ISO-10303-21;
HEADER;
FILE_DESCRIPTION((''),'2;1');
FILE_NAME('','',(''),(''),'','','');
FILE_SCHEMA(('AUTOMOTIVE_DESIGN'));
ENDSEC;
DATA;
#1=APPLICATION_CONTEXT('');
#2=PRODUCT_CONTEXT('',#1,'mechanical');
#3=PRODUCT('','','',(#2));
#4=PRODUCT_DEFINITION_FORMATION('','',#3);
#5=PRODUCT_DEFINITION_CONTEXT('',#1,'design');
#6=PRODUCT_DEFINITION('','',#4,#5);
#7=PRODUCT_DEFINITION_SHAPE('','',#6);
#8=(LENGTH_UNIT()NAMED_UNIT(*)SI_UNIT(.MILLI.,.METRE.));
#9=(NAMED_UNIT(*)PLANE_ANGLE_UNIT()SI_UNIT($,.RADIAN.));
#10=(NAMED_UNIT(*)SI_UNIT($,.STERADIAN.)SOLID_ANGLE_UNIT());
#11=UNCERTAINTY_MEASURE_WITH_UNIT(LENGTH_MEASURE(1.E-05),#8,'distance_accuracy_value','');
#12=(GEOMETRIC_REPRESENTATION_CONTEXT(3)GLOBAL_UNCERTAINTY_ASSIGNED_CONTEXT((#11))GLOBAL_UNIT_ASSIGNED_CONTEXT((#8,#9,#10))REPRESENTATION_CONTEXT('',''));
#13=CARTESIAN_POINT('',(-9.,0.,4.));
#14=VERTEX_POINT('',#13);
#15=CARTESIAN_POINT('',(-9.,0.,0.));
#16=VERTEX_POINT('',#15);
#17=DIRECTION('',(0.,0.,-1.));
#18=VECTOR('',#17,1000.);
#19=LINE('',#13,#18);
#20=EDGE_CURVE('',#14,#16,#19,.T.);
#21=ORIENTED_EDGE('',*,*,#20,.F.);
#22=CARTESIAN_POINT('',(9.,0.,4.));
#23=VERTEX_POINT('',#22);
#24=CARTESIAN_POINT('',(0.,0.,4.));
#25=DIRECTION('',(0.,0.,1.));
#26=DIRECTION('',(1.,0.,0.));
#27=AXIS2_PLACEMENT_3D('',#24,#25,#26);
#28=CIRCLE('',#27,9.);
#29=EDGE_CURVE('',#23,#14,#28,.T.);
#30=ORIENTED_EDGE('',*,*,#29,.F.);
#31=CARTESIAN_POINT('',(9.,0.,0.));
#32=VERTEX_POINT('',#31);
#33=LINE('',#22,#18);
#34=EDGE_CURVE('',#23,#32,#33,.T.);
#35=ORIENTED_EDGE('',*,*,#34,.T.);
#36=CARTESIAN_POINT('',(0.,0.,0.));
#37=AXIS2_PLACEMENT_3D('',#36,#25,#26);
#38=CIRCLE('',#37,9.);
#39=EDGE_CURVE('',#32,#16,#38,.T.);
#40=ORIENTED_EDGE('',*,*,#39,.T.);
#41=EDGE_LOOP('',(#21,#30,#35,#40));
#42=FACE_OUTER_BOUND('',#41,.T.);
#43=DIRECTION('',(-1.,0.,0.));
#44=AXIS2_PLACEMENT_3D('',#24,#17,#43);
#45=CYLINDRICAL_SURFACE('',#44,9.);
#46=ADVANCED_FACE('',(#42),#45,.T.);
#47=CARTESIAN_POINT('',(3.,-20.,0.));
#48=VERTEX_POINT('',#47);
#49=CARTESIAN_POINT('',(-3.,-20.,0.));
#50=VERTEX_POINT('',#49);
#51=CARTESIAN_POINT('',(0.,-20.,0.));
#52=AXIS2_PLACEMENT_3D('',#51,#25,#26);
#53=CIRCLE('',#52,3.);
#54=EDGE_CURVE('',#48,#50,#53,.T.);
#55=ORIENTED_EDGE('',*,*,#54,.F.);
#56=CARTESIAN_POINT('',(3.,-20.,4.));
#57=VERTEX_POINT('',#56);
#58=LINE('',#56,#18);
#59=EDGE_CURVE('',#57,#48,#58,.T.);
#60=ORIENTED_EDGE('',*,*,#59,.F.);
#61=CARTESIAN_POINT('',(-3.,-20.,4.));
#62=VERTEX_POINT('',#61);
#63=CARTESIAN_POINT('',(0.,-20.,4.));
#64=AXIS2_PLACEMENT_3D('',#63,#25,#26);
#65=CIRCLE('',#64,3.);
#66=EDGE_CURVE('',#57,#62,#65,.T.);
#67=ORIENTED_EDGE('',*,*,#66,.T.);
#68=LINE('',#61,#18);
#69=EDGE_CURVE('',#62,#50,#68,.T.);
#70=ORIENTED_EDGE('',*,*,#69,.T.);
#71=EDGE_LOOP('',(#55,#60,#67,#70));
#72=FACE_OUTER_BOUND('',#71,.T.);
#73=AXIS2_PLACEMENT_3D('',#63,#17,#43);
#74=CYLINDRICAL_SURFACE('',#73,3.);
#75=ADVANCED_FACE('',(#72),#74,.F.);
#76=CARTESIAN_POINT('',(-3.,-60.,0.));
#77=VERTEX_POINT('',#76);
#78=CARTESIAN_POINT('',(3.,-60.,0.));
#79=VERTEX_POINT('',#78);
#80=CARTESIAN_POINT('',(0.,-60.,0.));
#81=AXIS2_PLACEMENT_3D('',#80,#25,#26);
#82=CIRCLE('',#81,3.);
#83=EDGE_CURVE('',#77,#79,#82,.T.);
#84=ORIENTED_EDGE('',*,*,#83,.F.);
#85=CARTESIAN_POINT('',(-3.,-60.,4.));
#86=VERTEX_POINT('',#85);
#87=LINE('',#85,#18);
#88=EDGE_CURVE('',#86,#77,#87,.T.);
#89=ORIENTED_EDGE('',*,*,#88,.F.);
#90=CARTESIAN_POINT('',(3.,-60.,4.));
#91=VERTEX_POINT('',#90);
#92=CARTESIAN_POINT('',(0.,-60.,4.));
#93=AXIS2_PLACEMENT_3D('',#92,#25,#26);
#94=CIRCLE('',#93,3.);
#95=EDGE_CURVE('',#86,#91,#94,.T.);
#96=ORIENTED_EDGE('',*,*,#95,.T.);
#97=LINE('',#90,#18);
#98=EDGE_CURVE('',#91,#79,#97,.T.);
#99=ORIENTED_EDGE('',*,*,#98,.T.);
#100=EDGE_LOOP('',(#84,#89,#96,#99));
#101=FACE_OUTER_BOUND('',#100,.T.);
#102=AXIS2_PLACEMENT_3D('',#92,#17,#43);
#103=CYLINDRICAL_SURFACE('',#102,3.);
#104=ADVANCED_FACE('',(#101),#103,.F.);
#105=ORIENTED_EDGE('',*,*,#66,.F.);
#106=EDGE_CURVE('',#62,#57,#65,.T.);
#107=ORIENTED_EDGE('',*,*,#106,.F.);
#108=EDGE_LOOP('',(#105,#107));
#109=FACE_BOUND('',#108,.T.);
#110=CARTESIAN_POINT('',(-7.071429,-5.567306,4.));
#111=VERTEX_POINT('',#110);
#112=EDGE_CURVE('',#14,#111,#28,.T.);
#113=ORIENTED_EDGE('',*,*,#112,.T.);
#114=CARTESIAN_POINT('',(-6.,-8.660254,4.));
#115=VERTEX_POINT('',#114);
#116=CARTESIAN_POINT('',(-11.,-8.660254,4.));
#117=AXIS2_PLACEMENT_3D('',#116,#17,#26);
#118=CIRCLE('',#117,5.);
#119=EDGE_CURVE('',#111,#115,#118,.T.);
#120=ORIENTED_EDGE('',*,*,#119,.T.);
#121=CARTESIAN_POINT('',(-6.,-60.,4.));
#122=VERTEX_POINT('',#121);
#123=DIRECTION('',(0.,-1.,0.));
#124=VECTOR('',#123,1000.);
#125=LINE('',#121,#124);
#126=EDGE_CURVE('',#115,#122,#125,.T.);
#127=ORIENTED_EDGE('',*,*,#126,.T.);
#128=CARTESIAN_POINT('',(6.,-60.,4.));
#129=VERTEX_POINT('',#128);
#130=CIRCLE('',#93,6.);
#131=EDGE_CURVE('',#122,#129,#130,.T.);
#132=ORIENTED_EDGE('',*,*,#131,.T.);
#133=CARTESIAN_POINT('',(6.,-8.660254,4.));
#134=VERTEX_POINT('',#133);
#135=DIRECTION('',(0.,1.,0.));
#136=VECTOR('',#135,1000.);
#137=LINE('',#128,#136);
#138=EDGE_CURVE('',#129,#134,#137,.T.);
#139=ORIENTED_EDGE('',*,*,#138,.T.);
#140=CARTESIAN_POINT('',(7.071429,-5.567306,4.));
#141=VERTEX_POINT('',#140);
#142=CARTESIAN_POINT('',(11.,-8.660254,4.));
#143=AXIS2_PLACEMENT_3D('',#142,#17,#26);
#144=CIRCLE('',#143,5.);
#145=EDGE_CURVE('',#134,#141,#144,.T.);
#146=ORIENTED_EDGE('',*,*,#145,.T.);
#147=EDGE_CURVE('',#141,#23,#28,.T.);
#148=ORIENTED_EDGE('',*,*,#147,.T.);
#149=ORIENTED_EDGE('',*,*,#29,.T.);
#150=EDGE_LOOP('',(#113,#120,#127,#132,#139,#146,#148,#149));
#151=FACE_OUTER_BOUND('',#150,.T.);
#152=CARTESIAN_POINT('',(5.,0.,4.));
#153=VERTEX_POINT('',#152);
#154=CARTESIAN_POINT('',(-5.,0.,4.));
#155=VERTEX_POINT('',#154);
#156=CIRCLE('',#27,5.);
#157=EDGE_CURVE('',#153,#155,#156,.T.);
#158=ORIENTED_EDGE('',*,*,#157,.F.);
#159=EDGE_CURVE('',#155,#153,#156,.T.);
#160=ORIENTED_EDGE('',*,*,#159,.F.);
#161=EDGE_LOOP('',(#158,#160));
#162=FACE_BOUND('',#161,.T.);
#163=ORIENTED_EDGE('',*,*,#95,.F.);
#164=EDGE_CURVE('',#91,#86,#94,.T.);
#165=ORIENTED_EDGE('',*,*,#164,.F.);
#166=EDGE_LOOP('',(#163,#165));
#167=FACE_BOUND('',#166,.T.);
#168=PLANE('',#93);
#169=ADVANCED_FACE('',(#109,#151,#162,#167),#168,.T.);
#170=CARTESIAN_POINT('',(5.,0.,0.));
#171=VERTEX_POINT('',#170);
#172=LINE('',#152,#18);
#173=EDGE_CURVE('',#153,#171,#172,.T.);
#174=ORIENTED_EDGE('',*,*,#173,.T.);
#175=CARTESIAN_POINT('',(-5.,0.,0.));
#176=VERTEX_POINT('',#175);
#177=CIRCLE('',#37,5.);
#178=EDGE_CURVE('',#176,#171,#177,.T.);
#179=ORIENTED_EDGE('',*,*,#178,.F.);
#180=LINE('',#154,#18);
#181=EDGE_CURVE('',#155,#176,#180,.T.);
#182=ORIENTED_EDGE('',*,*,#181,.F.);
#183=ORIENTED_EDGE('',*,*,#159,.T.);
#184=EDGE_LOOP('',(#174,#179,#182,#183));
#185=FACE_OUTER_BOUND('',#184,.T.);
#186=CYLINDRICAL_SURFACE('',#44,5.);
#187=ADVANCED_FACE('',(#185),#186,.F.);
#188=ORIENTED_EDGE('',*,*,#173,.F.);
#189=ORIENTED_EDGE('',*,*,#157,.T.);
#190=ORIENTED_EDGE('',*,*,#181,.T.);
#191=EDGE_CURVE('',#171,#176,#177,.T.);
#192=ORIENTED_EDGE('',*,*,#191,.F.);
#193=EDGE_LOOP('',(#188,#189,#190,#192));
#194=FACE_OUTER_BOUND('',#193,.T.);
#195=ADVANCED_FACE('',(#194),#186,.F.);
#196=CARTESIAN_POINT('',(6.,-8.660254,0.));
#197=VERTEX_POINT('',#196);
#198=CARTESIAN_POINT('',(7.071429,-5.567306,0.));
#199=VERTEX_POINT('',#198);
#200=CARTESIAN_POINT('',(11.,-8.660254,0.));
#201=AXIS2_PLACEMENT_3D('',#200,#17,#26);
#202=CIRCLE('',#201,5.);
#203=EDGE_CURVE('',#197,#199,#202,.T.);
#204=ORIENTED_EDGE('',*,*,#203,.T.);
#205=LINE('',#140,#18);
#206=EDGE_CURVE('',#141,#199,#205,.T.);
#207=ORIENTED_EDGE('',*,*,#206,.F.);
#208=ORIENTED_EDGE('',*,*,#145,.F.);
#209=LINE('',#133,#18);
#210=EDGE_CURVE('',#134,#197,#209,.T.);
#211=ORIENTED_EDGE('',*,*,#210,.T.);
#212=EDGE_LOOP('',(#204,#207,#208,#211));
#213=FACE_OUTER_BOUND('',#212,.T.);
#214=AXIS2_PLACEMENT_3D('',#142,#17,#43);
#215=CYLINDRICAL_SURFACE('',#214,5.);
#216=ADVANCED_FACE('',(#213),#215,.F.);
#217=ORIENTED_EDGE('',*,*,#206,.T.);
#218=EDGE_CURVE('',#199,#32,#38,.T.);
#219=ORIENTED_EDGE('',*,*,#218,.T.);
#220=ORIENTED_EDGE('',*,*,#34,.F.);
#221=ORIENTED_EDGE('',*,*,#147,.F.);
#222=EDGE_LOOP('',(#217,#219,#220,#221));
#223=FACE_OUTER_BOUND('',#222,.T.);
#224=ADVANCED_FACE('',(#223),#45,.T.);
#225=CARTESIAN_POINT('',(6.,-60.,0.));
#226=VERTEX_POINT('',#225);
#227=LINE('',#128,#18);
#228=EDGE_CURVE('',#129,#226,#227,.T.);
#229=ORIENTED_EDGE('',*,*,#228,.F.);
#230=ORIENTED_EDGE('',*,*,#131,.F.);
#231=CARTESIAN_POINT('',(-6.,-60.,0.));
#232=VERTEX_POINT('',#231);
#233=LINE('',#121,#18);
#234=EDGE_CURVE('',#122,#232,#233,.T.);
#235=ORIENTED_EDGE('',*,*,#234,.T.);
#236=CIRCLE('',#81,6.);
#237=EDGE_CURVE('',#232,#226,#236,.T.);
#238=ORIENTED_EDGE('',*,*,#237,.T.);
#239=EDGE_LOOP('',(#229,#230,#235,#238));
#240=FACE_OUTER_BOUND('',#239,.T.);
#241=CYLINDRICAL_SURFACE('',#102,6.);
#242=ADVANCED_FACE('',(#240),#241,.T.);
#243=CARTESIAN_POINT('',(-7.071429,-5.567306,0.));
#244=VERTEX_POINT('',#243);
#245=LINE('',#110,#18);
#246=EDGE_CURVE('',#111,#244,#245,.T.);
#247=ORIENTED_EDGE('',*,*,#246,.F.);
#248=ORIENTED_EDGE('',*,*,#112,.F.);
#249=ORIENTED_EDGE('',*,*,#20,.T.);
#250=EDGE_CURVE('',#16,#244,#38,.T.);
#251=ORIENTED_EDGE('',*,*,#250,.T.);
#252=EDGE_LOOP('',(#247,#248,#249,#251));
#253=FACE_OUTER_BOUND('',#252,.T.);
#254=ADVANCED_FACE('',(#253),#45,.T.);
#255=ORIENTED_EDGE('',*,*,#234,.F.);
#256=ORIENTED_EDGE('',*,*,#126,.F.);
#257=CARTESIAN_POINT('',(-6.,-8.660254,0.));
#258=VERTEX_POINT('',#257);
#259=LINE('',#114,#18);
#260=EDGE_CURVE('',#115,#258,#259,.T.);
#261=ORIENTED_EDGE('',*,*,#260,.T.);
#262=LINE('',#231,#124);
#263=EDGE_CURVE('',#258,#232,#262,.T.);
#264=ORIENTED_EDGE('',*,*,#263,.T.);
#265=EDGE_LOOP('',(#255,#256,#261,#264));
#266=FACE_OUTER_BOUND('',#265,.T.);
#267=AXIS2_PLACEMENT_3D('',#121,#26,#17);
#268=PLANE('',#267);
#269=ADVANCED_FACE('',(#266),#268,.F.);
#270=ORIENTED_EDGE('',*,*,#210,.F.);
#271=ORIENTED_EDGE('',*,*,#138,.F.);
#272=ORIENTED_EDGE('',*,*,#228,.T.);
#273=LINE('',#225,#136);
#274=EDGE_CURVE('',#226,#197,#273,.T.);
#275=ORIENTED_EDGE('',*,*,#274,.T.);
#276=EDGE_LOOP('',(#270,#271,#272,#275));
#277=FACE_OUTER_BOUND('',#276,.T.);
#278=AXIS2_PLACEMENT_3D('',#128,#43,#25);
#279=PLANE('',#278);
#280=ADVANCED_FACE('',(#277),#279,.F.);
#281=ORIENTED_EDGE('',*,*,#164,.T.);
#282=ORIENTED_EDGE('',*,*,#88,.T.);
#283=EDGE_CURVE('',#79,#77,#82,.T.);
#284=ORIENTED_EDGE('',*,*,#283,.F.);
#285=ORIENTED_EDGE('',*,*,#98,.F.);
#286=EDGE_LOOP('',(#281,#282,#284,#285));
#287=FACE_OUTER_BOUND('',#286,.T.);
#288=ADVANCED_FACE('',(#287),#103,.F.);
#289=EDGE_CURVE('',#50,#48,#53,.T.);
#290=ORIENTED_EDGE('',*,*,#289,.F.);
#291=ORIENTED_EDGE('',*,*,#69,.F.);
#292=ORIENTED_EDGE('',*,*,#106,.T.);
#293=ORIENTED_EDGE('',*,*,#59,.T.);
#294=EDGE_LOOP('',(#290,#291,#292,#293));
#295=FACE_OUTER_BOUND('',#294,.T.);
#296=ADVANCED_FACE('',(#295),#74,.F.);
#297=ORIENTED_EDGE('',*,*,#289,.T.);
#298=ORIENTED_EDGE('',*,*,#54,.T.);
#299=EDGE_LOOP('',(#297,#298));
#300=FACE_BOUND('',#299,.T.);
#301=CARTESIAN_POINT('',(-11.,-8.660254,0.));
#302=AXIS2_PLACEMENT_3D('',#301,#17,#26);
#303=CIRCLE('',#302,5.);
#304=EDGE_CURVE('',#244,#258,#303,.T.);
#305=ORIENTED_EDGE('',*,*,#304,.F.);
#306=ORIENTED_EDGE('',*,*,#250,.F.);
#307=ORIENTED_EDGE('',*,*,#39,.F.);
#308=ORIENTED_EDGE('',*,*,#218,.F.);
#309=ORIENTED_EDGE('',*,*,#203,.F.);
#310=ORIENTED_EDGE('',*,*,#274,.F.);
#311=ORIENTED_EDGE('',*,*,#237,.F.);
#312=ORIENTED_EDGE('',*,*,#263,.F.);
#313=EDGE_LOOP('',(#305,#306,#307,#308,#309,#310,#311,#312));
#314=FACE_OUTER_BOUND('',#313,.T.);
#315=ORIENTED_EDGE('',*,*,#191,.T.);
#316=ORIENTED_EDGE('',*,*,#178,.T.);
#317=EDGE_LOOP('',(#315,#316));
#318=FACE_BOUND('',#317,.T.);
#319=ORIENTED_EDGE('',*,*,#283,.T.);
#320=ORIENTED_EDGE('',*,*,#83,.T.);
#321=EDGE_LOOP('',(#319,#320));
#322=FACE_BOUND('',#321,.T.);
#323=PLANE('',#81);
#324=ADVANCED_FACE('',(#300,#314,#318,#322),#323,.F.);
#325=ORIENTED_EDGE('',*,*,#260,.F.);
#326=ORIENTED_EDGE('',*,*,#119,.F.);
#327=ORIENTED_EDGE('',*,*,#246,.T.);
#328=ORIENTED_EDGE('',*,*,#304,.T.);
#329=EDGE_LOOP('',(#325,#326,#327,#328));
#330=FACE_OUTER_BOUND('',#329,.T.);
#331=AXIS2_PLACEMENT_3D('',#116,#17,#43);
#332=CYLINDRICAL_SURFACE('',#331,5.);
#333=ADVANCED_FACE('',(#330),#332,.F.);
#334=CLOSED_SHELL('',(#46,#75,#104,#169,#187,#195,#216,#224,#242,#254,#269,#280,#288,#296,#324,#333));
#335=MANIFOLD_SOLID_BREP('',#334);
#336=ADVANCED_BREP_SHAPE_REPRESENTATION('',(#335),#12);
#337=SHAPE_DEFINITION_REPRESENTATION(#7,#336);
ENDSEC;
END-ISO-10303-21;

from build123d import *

# Parameters (mm, degrees)
SKETCH1_R           = 5
SKETCH1_R_2         = 3
BOSS_EXTRUDE1_DEPTH = 4


with BuildPart() as part:
    # Sketch1 → Boss-Extrude1 (new body)
    with BuildSketch(Plane.XY):
        with BuildLine():
            Line((-6, -60), (-6, -8.660254038))
            ThreePointArc((-6, -8.660254038), (-6.275444087, -7.023619861), (-7.071428571, -5.567306167))
            ThreePointArc((-7.071428571, -5.567306167), (0, 9), (7.071428571, -5.567306167))
            ThreePointArc((7.071428571, -5.567306167), (6.275444087, -7.023619861), (6, -8.660254038))
            Line((6, -8.660254038), (6, -60))
            ThreePointArc((6, -60), (0, -66), (-6, -60))
        make_face()
        Circle(SKETCH1_R, mode=Mode.SUBTRACT)
        with Locations((0, -20)):
            Circle(SKETCH1_R_2, mode=Mode.SUBTRACT)
        with Locations((0, -60)):
            Circle(SKETCH1_R_2, mode=Mode.SUBTRACT)
    extrude(amount=BOSS_EXTRUDE1_DEPTH)


solid = part.part
